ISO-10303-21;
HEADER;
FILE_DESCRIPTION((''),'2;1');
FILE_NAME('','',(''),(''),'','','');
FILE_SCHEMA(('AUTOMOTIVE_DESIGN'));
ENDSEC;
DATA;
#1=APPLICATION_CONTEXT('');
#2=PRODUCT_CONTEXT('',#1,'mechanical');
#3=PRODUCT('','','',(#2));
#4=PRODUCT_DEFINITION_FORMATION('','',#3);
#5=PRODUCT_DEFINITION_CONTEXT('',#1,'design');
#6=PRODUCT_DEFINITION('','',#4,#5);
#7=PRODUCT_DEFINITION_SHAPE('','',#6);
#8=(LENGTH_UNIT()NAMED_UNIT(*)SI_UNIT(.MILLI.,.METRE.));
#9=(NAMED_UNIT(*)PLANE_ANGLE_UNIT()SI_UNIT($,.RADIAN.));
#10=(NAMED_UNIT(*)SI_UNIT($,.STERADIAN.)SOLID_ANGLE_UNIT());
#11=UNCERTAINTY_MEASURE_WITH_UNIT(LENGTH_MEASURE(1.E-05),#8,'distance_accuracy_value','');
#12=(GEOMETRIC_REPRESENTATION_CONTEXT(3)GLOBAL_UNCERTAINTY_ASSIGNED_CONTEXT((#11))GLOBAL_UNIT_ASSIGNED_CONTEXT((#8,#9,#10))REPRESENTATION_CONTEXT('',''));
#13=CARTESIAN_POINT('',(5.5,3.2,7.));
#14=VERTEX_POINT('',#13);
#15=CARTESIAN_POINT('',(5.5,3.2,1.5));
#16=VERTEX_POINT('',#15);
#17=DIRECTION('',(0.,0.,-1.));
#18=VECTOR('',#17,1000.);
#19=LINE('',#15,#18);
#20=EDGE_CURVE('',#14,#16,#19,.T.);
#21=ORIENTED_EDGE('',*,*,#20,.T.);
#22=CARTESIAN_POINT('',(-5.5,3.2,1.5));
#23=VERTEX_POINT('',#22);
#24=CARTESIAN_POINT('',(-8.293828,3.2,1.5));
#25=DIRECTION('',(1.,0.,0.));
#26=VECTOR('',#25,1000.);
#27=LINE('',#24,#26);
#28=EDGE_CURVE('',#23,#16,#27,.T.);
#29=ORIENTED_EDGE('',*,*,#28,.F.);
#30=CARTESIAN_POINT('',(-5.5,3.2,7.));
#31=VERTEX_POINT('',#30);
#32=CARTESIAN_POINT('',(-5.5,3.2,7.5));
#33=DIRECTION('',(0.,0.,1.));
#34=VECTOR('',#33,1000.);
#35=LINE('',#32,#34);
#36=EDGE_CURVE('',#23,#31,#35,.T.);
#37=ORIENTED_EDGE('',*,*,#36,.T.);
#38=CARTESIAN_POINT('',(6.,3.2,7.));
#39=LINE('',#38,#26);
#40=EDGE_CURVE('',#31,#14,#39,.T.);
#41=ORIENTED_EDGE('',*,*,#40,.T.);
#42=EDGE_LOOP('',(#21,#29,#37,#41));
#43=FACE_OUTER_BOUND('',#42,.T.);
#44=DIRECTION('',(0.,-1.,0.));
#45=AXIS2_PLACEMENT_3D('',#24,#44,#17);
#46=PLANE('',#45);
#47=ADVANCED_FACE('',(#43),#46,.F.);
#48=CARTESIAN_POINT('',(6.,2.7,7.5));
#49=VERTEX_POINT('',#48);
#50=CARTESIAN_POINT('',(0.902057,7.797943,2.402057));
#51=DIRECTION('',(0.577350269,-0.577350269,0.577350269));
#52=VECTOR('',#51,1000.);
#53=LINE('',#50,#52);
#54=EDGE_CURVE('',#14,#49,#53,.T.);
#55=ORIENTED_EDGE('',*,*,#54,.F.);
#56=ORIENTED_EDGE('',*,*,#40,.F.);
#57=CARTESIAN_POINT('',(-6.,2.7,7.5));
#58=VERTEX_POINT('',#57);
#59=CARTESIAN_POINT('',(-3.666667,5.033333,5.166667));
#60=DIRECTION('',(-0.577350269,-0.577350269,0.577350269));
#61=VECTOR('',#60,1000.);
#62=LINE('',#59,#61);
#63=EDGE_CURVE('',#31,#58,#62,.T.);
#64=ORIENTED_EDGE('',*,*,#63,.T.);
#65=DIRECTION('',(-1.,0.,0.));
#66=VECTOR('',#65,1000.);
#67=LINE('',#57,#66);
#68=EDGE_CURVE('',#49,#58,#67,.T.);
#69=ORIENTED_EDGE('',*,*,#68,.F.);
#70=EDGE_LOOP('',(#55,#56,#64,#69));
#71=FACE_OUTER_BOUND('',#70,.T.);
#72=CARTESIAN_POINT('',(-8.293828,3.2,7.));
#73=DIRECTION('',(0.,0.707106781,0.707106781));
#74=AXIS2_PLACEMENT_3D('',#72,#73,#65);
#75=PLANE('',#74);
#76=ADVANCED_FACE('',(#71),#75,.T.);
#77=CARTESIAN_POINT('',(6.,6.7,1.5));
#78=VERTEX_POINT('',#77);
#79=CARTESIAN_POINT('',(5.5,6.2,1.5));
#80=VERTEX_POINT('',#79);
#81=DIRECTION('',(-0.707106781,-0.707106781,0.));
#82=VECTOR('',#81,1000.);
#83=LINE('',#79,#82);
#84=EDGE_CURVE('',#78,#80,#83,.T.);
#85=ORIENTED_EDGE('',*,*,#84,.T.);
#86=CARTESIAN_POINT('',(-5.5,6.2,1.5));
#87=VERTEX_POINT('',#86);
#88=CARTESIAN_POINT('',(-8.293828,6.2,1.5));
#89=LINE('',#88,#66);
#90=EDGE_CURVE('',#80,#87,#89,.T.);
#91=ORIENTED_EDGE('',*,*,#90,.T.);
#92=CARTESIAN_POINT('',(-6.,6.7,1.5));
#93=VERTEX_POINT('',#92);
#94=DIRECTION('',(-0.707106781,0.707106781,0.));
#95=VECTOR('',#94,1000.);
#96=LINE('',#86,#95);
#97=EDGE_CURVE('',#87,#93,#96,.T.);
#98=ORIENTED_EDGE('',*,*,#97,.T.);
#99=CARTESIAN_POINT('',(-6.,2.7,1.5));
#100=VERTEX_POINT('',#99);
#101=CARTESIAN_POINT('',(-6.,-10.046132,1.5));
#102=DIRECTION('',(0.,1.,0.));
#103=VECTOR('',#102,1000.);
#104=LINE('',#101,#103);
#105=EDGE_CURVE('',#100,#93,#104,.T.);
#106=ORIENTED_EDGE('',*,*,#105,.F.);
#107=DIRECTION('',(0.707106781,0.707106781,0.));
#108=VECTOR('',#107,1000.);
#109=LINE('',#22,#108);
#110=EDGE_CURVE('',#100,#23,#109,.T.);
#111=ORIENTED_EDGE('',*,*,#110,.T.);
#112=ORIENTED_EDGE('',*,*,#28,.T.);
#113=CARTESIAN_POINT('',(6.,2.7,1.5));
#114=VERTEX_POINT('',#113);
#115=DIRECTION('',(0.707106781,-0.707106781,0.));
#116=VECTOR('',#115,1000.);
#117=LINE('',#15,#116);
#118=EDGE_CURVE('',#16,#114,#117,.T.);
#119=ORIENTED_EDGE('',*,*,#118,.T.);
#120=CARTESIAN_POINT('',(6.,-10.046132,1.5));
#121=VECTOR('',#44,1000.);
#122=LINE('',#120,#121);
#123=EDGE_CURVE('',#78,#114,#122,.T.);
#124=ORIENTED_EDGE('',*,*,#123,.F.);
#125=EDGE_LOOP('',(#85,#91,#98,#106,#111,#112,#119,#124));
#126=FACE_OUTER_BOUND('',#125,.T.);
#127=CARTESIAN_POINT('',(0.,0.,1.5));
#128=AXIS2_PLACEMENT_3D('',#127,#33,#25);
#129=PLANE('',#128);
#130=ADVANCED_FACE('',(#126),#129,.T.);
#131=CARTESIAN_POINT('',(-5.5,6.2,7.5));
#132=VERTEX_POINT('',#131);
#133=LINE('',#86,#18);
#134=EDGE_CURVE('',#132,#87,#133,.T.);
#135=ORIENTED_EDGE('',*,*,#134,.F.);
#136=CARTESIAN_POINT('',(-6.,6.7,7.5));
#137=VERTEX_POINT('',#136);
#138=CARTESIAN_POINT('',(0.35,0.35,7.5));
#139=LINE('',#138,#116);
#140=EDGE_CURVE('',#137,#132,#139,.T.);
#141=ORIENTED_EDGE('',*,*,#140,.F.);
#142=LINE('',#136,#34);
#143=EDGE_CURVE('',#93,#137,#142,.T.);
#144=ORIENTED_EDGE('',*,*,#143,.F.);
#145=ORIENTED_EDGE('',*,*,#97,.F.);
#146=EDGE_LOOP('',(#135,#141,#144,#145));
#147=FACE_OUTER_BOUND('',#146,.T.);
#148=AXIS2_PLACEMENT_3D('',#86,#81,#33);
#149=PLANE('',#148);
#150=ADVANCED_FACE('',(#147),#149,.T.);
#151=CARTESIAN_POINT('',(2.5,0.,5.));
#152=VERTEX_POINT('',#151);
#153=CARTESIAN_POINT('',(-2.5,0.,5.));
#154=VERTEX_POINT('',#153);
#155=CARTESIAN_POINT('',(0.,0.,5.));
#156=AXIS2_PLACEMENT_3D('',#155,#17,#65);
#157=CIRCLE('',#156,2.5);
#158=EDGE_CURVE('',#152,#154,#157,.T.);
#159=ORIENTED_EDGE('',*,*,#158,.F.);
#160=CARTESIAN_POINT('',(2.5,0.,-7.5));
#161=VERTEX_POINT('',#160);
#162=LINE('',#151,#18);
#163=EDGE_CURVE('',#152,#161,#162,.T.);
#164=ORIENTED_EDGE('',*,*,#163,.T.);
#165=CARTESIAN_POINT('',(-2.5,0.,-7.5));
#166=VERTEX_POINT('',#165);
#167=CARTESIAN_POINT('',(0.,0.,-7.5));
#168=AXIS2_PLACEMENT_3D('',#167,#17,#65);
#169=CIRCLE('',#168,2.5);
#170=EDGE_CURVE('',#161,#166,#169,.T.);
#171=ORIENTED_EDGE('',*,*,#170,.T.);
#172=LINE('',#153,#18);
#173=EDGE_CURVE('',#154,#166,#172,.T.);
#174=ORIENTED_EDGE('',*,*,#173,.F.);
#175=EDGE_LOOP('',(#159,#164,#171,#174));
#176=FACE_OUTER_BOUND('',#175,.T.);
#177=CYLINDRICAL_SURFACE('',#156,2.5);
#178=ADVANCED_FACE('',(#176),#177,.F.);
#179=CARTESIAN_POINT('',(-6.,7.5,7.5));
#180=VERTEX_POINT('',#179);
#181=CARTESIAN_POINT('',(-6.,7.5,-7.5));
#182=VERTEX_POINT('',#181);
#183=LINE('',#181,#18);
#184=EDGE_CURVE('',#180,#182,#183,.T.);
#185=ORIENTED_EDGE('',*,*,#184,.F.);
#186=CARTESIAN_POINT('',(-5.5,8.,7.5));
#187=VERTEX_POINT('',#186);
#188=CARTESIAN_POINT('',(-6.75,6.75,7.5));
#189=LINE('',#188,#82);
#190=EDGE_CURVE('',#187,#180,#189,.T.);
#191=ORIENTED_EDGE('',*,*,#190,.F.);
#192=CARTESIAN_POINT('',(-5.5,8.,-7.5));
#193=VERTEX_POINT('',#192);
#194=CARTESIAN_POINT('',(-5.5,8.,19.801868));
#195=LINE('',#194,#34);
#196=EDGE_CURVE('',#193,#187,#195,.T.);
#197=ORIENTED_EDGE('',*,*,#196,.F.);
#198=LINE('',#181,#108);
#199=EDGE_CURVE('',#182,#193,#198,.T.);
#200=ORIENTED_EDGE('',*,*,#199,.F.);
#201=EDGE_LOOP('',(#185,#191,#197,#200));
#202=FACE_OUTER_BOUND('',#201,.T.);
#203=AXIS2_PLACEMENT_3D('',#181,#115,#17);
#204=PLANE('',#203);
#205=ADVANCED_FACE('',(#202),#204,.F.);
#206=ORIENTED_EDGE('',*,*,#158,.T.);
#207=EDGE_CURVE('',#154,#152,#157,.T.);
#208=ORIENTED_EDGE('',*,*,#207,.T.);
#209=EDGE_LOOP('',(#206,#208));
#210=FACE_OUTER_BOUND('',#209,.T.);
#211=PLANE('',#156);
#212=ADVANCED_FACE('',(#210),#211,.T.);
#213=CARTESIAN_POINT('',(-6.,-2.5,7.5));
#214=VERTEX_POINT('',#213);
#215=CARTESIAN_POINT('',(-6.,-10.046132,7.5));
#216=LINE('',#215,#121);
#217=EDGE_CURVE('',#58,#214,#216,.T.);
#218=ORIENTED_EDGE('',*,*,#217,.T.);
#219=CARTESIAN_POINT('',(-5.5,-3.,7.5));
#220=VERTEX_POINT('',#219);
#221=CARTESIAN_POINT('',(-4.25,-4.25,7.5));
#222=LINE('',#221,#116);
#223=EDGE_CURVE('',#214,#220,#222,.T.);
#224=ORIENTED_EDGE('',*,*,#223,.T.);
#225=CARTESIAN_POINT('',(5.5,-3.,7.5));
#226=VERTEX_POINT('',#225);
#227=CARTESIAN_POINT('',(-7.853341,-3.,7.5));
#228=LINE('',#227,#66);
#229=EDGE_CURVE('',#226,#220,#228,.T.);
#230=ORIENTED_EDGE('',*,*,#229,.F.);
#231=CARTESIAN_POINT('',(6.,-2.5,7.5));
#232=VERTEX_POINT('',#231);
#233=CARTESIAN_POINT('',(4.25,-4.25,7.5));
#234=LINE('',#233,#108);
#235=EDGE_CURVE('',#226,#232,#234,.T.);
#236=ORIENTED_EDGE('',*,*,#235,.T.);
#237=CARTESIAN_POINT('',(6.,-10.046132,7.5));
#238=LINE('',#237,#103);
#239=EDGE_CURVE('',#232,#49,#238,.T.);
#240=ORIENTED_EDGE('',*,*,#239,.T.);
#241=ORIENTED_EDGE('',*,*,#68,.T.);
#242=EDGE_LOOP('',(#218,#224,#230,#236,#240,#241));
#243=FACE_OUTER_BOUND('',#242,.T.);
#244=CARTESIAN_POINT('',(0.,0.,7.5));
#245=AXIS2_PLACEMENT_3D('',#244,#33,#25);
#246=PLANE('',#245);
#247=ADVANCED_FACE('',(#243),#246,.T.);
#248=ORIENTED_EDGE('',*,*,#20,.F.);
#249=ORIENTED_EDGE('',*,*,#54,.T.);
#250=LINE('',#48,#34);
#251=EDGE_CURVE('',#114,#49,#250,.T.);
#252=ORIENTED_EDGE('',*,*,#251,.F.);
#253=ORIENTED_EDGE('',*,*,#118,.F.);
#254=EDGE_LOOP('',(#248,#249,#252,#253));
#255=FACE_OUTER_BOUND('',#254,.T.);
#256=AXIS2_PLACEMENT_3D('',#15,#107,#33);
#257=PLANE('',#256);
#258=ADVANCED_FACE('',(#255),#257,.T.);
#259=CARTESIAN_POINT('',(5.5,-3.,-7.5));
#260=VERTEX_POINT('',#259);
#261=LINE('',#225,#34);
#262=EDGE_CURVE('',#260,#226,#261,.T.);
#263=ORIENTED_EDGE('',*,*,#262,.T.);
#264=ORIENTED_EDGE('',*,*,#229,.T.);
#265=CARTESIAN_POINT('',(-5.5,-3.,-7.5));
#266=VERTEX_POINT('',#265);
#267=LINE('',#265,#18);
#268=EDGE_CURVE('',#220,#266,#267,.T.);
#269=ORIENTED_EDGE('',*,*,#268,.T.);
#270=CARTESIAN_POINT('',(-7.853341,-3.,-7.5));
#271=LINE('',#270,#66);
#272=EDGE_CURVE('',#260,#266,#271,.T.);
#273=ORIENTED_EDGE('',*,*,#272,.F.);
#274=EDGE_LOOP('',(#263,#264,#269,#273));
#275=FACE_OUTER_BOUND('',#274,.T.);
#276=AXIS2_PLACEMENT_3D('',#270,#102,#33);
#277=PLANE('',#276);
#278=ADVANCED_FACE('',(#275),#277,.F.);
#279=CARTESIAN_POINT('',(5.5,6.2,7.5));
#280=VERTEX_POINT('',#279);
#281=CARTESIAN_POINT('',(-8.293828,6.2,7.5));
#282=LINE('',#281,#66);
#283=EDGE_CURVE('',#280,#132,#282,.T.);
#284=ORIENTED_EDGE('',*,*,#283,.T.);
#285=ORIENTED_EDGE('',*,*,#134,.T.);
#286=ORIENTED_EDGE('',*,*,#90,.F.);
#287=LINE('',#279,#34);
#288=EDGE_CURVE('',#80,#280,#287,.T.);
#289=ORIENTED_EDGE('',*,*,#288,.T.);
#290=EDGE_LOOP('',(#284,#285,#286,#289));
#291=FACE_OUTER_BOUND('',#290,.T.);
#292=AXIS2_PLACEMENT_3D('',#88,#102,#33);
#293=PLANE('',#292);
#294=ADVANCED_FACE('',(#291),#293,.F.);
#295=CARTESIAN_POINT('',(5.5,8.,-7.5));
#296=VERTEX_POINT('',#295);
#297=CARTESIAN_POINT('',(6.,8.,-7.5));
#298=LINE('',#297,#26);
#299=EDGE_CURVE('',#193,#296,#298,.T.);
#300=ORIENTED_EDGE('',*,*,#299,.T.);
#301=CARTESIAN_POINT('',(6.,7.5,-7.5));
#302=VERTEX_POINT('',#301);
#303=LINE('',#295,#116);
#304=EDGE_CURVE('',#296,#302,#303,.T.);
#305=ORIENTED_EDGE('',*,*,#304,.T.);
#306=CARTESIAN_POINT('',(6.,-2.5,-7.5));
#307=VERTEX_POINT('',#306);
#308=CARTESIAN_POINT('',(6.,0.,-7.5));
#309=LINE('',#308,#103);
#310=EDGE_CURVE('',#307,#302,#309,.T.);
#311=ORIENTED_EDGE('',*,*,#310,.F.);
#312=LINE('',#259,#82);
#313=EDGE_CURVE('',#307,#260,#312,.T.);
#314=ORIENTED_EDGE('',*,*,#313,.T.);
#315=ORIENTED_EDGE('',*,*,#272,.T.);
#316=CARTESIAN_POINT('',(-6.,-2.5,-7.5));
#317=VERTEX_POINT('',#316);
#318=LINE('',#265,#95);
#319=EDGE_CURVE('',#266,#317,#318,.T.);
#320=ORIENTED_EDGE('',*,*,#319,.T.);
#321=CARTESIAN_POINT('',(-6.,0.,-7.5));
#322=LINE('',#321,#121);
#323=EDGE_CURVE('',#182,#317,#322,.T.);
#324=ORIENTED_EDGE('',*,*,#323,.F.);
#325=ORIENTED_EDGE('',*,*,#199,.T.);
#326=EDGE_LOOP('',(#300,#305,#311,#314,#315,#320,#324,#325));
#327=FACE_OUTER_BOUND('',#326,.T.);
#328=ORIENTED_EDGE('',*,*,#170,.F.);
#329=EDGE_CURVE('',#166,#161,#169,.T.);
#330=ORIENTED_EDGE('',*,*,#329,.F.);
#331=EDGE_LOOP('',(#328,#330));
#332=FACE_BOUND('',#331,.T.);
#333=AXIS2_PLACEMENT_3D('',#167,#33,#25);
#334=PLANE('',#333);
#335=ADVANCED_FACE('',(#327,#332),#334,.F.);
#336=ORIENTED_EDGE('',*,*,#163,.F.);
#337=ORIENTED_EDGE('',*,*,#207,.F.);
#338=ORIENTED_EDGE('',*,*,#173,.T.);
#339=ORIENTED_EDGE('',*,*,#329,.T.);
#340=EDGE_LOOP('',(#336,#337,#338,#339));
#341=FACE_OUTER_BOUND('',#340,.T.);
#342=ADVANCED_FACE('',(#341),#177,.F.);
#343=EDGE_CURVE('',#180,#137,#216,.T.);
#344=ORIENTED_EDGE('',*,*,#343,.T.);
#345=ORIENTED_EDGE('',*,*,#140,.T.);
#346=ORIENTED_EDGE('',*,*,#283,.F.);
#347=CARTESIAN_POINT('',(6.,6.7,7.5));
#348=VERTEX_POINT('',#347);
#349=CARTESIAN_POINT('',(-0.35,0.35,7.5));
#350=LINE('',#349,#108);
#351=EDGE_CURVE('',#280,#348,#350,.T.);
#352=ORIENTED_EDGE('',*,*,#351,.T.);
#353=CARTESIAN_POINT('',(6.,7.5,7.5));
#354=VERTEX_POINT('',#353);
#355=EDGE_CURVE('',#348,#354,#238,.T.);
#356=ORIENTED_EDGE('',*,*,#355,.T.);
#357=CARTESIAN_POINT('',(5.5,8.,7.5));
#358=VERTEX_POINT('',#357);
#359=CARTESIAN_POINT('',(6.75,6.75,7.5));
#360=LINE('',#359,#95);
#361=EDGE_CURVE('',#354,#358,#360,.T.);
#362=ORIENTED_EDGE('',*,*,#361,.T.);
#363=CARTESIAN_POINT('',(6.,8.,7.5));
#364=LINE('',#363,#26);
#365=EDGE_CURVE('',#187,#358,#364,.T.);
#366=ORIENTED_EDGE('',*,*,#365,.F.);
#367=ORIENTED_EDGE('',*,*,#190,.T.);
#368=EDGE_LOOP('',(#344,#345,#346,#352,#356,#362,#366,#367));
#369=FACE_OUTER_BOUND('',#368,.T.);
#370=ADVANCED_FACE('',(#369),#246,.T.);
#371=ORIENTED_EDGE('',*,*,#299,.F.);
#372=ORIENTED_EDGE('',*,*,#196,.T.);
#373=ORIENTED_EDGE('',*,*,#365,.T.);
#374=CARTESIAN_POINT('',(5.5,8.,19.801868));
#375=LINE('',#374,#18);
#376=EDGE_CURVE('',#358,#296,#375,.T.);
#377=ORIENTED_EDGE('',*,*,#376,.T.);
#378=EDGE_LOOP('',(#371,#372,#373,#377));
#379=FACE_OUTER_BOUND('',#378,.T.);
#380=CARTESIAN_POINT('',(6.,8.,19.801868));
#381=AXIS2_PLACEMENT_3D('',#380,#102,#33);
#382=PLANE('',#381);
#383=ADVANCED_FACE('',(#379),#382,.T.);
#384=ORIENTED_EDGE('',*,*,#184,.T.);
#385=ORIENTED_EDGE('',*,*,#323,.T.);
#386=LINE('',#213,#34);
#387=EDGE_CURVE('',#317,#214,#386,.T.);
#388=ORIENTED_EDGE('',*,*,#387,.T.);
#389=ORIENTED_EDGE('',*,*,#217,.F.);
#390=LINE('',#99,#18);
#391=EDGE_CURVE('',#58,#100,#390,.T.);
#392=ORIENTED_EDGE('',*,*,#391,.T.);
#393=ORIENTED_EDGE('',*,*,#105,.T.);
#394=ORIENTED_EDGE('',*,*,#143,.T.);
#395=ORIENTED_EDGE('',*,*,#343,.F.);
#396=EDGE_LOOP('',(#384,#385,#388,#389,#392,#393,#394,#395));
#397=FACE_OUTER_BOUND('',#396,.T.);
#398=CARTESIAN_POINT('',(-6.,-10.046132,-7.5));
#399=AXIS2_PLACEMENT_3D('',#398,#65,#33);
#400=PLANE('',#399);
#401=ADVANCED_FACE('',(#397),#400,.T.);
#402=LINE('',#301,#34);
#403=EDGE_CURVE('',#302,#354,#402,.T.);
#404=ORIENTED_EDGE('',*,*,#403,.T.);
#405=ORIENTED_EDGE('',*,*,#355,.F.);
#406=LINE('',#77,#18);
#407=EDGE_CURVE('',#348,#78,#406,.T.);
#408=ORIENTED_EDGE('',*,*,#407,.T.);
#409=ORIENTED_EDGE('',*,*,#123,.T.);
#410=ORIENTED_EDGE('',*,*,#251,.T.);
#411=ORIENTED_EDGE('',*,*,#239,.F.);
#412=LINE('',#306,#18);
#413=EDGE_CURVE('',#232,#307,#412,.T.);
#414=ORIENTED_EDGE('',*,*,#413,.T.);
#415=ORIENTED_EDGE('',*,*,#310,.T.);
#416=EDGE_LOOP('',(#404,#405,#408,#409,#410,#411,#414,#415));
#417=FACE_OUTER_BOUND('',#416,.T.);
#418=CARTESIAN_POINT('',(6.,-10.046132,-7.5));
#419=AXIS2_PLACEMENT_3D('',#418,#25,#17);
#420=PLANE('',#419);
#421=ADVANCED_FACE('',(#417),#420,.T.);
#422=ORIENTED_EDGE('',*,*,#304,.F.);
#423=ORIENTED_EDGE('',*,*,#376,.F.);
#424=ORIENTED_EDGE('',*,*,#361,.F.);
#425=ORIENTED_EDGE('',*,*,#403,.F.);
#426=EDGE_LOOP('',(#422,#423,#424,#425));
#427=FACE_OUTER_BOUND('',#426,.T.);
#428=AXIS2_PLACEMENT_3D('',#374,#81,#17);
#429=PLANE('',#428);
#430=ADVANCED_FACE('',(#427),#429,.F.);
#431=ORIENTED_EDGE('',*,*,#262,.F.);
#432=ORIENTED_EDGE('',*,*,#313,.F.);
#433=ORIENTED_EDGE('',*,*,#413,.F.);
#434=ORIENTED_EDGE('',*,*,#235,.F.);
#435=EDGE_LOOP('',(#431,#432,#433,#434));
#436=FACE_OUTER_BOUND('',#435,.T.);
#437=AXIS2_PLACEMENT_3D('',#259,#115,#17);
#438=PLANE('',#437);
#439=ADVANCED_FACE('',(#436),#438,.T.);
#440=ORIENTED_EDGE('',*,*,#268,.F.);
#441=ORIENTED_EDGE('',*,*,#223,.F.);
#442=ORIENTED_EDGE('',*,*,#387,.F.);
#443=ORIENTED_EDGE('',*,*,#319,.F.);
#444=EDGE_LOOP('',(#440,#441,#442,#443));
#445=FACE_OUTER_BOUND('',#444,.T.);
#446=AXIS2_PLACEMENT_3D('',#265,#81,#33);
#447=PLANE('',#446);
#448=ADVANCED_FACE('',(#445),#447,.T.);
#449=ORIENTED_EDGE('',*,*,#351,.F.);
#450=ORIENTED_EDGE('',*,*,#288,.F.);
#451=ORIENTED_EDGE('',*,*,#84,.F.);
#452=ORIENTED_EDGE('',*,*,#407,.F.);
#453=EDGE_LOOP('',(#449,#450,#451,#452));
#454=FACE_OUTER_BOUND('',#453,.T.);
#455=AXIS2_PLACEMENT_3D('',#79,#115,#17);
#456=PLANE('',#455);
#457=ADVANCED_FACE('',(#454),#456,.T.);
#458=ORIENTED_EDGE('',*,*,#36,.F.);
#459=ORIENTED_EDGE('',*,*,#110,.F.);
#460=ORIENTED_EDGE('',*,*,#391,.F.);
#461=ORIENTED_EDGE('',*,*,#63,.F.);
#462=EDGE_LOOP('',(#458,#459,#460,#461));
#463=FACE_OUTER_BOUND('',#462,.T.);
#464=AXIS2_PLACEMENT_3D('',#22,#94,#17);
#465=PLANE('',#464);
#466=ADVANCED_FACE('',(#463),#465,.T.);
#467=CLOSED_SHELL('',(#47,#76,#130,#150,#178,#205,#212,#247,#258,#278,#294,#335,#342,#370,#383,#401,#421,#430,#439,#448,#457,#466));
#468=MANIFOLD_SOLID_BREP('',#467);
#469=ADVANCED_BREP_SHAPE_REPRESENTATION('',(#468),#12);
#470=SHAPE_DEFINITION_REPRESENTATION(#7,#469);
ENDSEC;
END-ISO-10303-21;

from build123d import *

# Parameters (mm, degrees)
SKETCH_1_R           = 8
EXTRUDE_1_DEPTH      = 7.5
SKETCH_3_R           = 2.5
CUT_EXTRUDE_2_DEPTH  = 12.5
SKETCH_4_OUTSIDE_W   = 23.43
SKETCH_4_OUTSIDE_H   = 23.43
SKETCH_4_OUTSIDE_W_2 = 12
SKETCH_4_OUTSIDE_H_2 = 20.092263618
CUT_EXTRUDE_3_DEPTH  = 19.788294228
SKETCH_5_W           = 16.185662541
SKETCH_5_H           = 6.325725708
CUT_EXTRUDE_4_DEPTH  = 19.027756377
SKETCH_8_W           = 12
SKETCH_8_H           = 2.708497378
EXTRUDE_2_DEPTH      = 15
CHAMFER_1_SIZE       = 0.5
SKETCH_2_W           = 17
SKETCH_2_H           = 3
CUT_EXTRUDE_5_DEPTH  = 6
CHAMFER_2_SIZE       = 0.5


with BuildPart() as part:
    # 草图1 → 凸台-拉伸1 (new, symmetric)
    with BuildSketch(Plane.XY):
        Circle(SKETCH_1_R)
    extrude(amount=EXTRUDE_1_DEPTH, both=True)

    # 草图3 → 切除-拉伸2 (cut)
    with BuildSketch(Plane(origin=(0, 0, -7.5), x_dir=(-1, 0, 0), z_dir=(0, 0, -1))):
        Circle(SKETCH_3_R)
    extrude(amount=-CUT_EXTRUDE_2_DEPTH, mode=Mode.SUBTRACT)

    # 草图4 outside → 切除-拉伸3 (cut, through all)
    with BuildSketch(Plane.XY.offset(7.5)):
        Rectangle(SKETCH_4_OUTSIDE_W, SKETCH_4_OUTSIDE_H)
        Rectangle(SKETCH_4_OUTSIDE_W_2, SKETCH_4_OUTSIDE_H_2, mode=Mode.SUBTRACT)
    extrude(amount=-CUT_EXTRUDE_3_DEPTH, mode=Mode.SUBTRACT)

    # 草图5 → 切除-拉伸4 (cut, through all)
    with BuildSketch(Plane.XY.offset(7.5)):
        with Locations((0.239490277, -6.162862854)):
            Rectangle(SKETCH_5_W, SKETCH_5_H)
    extrude(amount=-CUT_EXTRUDE_4_DEPTH, mode=Mode.SUBTRACT)

    # 草图8 → 凸台-拉伸2 (add)
    with BuildSketch(Plane(origin=(0, 0, -7.5), x_dir=(-1, 0, 0), z_dir=(0, 0, -1))):
        with Locations((0, 6.645751311)):
            Rectangle(SKETCH_8_W, SKETCH_8_H)
    extrude(amount=-EXTRUDE_2_DEPTH)

    # 倒角1
    chamfer_1_edges = [part.edges().sort_by_distance(p)[0] for p in [
        (6, -3, 0),
        (-6, -3, 0),
        (6, 8, 0),
        (-6, 8, 0),
    ]]
    chamfer(chamfer_1_edges, length=CHAMFER_1_SIZE)

    # 草图2 → 切除-拉伸5 (cut)
    with BuildSketch(Plane.XY.offset(7.5)):
        with Locations((0.206171625, 4.7)):
            Rectangle(SKETCH_2_W, SKETCH_2_H)
    extrude(amount=-CUT_EXTRUDE_5_DEPTH, mode=Mode.SUBTRACT)

    # 倒角2
    chamfer_2_edges = [part.edges().sort_by_distance(p)[0] for p in [
        (6, 3.2, 4.5),
        (6, 6.2, 4.5),
        (-6, 6.2, 4.5),
        (-6, 3.2, 4.5),
        (0, 3.2, 7.5),
    ]]
    chamfer(chamfer_2_edges, length=CHAMFER_2_SIZE)


solid = part.part
